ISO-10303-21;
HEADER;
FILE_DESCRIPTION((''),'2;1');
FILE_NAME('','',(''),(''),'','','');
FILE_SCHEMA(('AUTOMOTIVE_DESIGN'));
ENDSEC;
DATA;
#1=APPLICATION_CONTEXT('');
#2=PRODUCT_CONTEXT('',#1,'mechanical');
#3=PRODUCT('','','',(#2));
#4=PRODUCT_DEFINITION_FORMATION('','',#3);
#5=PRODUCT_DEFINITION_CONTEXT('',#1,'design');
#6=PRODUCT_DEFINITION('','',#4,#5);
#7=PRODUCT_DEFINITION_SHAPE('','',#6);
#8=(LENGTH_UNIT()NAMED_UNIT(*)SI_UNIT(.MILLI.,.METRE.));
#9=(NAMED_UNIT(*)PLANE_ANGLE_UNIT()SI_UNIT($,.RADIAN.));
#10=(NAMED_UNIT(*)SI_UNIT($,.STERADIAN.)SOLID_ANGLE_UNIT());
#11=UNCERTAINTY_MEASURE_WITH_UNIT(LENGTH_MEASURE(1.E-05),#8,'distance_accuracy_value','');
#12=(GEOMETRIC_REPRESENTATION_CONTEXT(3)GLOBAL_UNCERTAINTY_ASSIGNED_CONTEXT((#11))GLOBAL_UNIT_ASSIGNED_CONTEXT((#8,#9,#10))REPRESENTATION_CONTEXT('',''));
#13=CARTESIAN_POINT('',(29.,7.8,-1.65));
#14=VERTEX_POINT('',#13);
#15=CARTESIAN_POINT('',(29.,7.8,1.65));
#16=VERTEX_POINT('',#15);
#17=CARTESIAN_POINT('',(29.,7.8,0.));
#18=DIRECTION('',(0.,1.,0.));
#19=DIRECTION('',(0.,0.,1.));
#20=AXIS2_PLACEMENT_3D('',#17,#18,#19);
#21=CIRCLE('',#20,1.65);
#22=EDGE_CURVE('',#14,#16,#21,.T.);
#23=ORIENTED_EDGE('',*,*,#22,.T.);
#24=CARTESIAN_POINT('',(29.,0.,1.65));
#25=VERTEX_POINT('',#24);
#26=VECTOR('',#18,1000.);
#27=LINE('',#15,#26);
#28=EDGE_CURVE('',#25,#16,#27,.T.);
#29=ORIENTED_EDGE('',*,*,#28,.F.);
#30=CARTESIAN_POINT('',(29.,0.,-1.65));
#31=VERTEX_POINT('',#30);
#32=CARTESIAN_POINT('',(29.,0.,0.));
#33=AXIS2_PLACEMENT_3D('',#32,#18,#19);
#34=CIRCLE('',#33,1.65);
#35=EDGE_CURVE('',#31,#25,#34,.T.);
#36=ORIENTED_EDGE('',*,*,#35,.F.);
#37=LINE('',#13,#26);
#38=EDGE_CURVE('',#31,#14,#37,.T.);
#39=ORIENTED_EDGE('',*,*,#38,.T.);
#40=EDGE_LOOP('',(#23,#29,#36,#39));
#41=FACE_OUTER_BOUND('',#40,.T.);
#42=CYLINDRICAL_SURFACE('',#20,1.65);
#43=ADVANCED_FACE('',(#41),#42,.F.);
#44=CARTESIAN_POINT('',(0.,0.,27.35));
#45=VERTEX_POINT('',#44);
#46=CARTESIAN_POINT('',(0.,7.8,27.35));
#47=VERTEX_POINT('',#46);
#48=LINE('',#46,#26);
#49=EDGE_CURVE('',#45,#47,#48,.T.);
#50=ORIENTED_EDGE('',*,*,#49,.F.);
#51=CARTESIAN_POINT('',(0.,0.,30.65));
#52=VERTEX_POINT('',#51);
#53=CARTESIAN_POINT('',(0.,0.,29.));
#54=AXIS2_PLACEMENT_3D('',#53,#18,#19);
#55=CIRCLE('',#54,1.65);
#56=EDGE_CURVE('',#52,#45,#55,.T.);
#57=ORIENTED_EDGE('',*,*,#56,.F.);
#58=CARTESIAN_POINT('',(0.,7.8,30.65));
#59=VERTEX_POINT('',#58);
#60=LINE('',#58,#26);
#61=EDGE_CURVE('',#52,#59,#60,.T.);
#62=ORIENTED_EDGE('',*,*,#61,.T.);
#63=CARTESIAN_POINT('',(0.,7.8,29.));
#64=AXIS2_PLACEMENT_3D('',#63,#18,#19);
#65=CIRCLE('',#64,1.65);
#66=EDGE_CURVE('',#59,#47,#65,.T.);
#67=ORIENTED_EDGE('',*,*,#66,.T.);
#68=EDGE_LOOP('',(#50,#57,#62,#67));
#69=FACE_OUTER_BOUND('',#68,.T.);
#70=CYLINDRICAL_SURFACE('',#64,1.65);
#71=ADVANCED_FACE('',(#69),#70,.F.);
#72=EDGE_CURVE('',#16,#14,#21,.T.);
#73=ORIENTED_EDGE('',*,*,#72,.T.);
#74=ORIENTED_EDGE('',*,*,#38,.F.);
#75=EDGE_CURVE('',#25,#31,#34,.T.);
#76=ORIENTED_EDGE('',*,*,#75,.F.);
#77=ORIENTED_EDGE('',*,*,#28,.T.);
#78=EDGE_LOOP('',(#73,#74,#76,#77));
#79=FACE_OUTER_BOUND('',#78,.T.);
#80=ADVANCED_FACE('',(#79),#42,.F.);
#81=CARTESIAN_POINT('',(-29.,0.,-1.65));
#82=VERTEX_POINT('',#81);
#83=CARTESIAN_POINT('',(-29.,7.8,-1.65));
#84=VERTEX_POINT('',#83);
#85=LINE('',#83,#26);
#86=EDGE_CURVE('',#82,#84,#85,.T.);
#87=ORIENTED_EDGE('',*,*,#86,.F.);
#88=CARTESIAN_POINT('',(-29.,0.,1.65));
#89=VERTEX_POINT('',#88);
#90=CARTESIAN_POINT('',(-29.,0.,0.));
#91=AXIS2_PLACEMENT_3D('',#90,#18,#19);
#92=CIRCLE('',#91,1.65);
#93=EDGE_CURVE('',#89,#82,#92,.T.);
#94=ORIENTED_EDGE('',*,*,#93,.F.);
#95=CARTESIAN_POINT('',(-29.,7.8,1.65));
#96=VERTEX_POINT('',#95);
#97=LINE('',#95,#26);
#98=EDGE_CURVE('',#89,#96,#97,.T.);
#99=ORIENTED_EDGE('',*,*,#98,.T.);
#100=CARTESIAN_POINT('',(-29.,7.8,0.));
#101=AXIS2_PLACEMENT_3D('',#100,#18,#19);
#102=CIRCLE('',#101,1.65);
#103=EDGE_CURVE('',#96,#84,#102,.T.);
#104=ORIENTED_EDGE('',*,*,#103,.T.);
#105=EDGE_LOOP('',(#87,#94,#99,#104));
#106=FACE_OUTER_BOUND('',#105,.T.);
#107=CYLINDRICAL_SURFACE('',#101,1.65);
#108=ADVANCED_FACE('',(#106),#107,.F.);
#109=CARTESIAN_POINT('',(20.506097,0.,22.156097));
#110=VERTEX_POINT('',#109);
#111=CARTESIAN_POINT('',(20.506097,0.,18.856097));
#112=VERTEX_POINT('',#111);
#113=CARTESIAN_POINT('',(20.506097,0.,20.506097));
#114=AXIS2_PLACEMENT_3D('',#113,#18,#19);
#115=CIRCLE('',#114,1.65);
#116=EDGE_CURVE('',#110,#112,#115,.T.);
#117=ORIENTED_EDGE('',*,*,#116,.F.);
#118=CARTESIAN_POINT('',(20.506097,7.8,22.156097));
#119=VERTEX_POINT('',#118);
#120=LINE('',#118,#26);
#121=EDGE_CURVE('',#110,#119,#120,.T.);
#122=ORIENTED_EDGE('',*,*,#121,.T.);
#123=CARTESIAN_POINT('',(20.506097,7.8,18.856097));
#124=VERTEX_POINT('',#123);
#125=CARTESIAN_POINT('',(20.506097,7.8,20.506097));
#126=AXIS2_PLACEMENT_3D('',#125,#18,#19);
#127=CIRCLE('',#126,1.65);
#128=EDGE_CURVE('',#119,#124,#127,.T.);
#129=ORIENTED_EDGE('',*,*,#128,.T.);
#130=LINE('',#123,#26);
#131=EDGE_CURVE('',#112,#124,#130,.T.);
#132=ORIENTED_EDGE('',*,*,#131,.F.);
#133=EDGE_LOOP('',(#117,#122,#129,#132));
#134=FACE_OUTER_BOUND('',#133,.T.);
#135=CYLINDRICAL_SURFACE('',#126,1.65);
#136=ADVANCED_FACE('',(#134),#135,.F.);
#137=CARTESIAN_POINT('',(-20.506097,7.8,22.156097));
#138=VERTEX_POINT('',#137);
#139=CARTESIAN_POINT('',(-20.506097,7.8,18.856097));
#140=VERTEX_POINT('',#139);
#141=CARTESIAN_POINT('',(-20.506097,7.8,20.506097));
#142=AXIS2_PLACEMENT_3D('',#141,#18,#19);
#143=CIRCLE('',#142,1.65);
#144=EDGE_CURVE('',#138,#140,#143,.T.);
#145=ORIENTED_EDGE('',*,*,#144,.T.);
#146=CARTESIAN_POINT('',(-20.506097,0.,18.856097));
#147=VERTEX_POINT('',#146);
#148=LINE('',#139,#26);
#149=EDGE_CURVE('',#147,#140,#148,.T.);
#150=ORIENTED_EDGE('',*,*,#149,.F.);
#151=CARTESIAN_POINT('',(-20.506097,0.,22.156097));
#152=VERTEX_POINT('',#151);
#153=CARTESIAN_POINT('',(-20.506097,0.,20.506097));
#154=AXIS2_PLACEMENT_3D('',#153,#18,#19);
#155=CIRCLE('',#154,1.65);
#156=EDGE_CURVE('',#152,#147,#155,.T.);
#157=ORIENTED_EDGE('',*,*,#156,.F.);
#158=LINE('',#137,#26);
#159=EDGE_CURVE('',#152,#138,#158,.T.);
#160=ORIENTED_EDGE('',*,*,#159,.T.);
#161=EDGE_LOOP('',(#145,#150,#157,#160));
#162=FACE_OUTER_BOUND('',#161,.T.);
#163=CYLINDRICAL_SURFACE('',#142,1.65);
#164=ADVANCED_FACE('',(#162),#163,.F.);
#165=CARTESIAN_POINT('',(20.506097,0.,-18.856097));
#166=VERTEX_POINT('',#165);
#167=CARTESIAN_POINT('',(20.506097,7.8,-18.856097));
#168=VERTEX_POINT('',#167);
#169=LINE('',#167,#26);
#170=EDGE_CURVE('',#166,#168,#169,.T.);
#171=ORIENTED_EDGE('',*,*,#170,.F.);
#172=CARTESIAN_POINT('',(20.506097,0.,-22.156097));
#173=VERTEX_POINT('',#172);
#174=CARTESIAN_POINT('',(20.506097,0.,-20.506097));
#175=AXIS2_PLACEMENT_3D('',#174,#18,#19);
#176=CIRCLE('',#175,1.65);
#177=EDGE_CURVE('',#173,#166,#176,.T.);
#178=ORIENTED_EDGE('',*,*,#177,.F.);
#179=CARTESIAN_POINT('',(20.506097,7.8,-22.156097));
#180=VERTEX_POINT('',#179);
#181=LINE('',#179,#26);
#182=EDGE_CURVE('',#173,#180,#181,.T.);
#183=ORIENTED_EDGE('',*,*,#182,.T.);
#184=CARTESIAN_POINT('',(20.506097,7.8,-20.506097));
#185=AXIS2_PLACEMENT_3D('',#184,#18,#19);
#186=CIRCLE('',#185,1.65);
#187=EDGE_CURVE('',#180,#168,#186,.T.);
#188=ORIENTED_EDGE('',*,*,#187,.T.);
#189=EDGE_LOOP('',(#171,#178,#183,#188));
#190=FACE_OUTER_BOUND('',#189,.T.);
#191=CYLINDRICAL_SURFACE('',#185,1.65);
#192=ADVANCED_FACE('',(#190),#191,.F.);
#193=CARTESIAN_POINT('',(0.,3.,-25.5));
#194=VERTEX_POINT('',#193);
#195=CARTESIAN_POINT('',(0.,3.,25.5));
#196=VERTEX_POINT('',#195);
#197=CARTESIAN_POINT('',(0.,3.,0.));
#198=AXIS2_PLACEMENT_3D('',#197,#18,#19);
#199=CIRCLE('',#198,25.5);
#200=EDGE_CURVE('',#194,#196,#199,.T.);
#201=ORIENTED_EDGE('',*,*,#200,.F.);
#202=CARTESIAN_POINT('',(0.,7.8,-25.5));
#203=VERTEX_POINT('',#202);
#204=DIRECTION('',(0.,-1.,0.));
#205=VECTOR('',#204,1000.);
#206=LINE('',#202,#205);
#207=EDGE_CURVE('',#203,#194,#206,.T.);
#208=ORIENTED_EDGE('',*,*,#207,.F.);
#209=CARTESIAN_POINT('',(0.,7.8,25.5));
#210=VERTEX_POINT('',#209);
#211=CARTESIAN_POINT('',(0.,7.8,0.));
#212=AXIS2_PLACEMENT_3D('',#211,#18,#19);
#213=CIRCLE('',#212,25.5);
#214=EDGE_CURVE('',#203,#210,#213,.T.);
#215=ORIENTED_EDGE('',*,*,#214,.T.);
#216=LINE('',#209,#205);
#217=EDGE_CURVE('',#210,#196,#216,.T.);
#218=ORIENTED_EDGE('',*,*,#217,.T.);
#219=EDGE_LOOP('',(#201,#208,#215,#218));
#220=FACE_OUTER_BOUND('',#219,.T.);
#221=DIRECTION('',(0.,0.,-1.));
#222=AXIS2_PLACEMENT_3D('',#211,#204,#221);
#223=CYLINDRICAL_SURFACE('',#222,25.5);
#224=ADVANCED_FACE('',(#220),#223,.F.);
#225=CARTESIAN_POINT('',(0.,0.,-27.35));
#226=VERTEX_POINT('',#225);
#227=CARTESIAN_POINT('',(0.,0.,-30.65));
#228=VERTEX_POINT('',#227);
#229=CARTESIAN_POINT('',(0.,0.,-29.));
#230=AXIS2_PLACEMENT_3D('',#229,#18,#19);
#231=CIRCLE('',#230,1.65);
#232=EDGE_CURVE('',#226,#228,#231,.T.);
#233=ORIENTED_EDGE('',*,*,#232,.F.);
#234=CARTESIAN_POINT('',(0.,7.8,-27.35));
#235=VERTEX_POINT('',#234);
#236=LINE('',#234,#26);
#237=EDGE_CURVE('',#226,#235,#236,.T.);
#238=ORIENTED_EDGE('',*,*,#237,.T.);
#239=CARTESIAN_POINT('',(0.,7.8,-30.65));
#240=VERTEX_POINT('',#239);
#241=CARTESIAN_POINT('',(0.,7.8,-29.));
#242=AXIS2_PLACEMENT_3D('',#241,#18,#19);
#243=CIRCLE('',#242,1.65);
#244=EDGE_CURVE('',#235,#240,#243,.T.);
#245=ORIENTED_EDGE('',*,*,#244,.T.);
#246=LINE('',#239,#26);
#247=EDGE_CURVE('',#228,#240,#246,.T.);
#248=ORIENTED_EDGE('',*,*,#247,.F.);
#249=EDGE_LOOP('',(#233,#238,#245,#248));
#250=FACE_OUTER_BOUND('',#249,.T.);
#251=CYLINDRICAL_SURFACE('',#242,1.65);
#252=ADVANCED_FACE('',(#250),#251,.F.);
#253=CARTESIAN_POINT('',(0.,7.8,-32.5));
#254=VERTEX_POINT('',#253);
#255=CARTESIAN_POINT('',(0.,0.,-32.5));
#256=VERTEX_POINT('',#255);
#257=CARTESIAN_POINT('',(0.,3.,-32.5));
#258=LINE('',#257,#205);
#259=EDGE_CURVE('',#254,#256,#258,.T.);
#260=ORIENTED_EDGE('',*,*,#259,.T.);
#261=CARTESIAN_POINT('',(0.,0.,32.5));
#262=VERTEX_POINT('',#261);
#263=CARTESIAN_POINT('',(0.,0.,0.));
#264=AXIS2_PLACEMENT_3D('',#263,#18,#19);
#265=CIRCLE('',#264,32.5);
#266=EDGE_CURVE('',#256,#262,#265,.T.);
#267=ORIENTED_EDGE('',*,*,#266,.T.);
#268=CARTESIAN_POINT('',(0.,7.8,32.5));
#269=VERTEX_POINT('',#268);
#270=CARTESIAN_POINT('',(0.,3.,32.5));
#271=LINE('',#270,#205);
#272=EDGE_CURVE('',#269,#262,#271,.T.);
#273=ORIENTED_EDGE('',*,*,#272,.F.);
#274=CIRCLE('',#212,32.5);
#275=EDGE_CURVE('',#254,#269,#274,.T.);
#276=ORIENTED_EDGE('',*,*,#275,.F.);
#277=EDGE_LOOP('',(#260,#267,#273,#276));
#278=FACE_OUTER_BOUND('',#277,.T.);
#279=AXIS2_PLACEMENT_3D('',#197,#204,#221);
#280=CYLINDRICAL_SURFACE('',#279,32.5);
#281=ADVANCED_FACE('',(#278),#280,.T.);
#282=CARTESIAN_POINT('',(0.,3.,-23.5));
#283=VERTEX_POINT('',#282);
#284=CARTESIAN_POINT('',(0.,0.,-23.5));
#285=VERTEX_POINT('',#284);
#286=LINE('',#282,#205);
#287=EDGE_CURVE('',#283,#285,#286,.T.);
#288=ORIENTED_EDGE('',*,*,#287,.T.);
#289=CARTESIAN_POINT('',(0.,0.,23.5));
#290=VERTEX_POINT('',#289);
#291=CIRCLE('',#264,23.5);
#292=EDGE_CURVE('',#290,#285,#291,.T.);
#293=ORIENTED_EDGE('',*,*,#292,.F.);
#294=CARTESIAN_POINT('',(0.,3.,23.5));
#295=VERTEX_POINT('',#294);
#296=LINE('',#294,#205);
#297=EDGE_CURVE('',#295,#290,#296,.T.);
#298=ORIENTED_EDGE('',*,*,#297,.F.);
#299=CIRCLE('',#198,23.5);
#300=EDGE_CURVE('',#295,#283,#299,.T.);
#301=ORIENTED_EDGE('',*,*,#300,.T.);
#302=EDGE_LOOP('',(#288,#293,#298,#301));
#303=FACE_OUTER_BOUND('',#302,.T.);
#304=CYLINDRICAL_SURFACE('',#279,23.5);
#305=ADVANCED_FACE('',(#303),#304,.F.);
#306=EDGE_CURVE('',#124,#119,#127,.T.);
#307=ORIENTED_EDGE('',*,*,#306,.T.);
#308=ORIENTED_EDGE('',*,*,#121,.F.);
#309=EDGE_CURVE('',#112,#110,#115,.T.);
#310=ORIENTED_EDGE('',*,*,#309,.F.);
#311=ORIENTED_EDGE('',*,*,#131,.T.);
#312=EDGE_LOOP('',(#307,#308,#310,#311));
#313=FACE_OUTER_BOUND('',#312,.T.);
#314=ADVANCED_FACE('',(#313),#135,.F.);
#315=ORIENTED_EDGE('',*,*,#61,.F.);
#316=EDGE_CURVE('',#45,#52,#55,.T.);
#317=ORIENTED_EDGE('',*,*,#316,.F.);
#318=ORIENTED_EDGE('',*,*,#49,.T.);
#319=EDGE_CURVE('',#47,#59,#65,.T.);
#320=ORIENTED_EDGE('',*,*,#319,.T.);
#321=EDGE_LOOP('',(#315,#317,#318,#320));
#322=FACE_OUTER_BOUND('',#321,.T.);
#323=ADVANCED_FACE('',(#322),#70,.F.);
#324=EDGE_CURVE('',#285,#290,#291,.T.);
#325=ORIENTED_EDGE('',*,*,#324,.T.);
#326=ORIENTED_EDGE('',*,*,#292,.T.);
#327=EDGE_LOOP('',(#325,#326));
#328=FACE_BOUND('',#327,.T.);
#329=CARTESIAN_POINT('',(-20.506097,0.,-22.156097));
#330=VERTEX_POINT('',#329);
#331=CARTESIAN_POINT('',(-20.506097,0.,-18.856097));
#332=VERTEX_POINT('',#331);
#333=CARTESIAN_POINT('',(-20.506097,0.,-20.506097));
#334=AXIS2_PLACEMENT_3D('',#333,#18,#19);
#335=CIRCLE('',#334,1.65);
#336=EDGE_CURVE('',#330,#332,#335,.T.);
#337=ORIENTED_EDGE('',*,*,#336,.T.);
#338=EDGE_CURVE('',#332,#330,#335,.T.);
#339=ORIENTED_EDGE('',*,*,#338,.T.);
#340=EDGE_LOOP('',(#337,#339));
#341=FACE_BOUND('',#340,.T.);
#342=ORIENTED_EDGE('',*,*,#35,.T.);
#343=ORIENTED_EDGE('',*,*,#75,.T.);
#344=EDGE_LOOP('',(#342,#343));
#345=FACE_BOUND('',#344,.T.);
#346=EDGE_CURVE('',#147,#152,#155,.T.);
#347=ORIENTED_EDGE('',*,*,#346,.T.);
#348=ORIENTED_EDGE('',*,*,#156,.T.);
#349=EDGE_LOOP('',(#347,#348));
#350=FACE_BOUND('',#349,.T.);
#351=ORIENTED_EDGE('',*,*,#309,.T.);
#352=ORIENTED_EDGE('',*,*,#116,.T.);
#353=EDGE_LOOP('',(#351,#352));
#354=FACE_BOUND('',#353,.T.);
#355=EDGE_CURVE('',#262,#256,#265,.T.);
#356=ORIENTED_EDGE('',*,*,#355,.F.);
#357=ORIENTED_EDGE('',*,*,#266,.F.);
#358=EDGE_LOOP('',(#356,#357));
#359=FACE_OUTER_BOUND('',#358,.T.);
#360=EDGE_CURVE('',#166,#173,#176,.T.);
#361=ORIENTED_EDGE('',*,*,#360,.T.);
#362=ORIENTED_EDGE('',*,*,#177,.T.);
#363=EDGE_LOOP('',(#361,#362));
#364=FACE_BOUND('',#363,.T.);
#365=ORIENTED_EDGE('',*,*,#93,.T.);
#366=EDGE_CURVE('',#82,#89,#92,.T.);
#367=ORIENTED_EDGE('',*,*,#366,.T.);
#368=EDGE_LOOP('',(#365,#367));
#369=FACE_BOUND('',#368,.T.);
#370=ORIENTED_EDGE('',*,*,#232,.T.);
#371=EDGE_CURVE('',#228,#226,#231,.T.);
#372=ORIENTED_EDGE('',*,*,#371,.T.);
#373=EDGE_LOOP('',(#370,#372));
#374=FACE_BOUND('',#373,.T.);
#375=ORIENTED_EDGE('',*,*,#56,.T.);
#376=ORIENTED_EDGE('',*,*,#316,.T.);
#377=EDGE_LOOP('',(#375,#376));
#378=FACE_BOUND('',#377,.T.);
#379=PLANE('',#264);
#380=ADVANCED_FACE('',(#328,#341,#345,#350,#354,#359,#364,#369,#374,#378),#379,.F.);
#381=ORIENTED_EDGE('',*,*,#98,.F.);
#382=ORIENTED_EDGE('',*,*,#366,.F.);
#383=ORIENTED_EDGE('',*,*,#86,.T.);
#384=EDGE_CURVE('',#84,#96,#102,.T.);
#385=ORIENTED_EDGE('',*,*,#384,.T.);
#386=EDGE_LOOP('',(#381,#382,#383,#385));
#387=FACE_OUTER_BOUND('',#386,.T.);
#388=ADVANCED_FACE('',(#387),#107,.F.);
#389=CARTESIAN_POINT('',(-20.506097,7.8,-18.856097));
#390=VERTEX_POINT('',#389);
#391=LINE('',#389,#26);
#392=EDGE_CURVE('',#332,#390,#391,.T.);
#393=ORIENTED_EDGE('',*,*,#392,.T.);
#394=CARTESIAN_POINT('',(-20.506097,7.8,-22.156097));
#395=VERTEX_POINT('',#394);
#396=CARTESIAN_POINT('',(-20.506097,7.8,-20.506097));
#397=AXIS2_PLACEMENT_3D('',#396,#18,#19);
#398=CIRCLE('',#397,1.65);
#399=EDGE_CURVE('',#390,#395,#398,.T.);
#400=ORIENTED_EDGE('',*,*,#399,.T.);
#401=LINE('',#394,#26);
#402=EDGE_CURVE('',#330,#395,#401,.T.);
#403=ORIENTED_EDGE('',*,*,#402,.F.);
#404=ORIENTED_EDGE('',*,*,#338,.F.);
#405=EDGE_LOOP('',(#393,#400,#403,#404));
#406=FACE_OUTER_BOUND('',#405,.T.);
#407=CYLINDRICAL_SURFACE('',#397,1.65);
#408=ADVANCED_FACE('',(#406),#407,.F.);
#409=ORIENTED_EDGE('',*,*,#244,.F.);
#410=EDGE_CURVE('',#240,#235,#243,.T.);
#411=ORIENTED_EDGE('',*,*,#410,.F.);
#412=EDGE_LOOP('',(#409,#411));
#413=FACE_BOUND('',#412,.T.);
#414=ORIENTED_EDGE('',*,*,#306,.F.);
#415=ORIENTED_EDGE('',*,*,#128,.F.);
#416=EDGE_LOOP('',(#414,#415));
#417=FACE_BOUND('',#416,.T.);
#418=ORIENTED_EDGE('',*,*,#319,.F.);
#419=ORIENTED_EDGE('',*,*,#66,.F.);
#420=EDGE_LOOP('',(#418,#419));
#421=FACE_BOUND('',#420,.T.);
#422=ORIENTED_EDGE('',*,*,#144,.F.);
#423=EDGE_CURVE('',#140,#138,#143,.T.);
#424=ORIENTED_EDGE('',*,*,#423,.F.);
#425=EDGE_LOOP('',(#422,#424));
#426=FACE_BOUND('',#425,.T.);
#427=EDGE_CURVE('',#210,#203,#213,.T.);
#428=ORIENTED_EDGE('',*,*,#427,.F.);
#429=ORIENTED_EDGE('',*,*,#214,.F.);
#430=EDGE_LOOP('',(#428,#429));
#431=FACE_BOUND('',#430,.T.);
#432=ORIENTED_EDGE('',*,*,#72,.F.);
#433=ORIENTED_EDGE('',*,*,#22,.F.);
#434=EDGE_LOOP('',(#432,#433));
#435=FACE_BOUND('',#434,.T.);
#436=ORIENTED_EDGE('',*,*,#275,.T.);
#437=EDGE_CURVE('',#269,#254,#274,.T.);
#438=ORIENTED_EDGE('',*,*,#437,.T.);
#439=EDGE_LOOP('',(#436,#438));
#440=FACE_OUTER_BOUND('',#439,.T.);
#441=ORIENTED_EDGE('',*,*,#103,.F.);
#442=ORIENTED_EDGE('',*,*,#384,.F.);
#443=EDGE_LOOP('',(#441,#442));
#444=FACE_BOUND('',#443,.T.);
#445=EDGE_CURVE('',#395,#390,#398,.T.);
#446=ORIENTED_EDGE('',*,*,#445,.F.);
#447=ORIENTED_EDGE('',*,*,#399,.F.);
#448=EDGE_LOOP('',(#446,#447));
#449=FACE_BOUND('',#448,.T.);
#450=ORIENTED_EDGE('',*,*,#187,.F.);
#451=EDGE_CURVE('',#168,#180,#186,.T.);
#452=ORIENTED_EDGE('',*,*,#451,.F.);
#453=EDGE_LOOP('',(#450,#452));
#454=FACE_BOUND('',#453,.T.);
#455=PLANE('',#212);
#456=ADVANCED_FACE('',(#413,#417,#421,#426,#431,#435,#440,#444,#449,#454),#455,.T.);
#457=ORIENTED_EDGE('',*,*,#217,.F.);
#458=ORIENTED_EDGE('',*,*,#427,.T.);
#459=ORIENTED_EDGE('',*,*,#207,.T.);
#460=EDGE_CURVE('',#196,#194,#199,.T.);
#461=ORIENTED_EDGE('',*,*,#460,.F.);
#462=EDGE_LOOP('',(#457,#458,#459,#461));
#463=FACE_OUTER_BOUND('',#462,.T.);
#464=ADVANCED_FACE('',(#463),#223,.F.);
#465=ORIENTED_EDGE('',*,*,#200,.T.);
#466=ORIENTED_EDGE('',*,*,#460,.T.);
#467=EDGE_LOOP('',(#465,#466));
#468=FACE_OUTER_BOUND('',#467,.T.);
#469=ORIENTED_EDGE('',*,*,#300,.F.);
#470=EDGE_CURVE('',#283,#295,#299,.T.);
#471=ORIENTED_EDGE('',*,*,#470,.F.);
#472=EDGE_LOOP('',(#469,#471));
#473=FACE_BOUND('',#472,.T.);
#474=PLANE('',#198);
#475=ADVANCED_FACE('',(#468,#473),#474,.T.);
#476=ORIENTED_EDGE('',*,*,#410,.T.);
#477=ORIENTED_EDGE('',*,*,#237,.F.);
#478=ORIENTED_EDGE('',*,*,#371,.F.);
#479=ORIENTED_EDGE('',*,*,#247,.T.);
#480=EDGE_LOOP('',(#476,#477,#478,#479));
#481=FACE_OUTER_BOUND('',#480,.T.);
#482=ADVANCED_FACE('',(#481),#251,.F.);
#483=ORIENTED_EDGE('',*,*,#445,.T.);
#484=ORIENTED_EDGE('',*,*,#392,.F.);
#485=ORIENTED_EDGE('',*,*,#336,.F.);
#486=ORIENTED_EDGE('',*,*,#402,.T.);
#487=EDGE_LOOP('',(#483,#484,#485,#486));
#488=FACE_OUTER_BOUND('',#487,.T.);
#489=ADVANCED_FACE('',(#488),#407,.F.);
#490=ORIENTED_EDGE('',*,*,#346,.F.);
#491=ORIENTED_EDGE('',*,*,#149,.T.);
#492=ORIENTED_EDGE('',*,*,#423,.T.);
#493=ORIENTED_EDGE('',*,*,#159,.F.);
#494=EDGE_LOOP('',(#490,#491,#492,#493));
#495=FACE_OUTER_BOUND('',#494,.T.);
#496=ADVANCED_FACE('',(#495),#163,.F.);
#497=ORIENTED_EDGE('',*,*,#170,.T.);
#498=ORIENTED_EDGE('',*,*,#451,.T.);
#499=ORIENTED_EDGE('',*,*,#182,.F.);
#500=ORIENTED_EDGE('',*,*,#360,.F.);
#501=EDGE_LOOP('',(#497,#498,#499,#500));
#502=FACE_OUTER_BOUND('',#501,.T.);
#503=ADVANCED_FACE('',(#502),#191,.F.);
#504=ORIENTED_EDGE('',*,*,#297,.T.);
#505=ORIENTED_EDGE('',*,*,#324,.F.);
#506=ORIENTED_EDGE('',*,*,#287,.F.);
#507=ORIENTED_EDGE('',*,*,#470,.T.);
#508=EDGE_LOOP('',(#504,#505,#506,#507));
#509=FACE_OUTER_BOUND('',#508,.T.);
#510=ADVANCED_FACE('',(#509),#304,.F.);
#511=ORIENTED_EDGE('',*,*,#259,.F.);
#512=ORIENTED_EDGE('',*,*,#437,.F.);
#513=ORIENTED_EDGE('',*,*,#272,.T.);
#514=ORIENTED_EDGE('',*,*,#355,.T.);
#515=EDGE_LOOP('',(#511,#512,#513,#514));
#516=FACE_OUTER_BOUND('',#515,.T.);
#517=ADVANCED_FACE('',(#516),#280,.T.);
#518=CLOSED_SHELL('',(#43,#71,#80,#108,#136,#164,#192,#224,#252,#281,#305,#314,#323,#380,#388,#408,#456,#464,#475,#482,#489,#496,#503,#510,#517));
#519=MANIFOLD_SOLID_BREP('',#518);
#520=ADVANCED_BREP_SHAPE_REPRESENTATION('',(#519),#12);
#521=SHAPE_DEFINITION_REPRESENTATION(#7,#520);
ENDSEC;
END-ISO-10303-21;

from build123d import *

# Parameters (mm, degrees)
SKETCH_1_R         = 32.5
SKETCH_1_R_2       = 23.5
EXTRUDE_1_DEPTH    = 3
SKETCH_2_R         = 32.5
SKETCH_2_R_2       = 25.5
EXTRUDE_2_DEPTH    = 4.8
HOLE_WIZARD_M4_1_D = 3.3


with BuildPart() as part:
    # 草图1 → 凸台-拉伸1 (new body)
    with BuildSketch(Plane(origin=(0, 0, 0), x_dir=(1, 0, 0), z_dir=(0, 1, 0))):
        with Locations(Location((0, 0, 0), (0, 0, 270))):
            Circle(SKETCH_1_R)
        with Locations(Location((0, 0, 0), (0, 0, 270))):
            Circle(SKETCH_1_R_2, mode=Mode.SUBTRACT)
    extrude(amount=EXTRUDE_1_DEPTH)

    # 草图2 → 凸台-拉伸2 (add)
    with BuildSketch(Plane(origin=(0, 3, 0), x_dir=(1, 0, 0), z_dir=(0, 1, 0))):
        with Locations(Location((0, 0, 0), (0, 0, 270))):
            Circle(SKETCH_2_R)
        with Locations(Location((0, 0, 0), (0, 0, 270))):
            Circle(SKETCH_2_R_2, mode=Mode.SUBTRACT)
    extrude(amount=EXTRUDE_2_DEPTH)

    # M4 螺纹孔1 (through all)
    with Locations(Plane(origin=(0, 7.8, 0), x_dir=(1, 0, 0), z_dir=(0, 1, 0))):
        with Locations((0, 29), (20.506096654, 20.506096654), (29, 0), (20.506096654, -20.506096654), (0, -29), (-20.506096654, -20.506096654), (-29, 0), (-20.506096654, 20.506096654), (0, 0)):
            Hole(HOLE_WIZARD_M4_1_D / 2)


solid = part.part
